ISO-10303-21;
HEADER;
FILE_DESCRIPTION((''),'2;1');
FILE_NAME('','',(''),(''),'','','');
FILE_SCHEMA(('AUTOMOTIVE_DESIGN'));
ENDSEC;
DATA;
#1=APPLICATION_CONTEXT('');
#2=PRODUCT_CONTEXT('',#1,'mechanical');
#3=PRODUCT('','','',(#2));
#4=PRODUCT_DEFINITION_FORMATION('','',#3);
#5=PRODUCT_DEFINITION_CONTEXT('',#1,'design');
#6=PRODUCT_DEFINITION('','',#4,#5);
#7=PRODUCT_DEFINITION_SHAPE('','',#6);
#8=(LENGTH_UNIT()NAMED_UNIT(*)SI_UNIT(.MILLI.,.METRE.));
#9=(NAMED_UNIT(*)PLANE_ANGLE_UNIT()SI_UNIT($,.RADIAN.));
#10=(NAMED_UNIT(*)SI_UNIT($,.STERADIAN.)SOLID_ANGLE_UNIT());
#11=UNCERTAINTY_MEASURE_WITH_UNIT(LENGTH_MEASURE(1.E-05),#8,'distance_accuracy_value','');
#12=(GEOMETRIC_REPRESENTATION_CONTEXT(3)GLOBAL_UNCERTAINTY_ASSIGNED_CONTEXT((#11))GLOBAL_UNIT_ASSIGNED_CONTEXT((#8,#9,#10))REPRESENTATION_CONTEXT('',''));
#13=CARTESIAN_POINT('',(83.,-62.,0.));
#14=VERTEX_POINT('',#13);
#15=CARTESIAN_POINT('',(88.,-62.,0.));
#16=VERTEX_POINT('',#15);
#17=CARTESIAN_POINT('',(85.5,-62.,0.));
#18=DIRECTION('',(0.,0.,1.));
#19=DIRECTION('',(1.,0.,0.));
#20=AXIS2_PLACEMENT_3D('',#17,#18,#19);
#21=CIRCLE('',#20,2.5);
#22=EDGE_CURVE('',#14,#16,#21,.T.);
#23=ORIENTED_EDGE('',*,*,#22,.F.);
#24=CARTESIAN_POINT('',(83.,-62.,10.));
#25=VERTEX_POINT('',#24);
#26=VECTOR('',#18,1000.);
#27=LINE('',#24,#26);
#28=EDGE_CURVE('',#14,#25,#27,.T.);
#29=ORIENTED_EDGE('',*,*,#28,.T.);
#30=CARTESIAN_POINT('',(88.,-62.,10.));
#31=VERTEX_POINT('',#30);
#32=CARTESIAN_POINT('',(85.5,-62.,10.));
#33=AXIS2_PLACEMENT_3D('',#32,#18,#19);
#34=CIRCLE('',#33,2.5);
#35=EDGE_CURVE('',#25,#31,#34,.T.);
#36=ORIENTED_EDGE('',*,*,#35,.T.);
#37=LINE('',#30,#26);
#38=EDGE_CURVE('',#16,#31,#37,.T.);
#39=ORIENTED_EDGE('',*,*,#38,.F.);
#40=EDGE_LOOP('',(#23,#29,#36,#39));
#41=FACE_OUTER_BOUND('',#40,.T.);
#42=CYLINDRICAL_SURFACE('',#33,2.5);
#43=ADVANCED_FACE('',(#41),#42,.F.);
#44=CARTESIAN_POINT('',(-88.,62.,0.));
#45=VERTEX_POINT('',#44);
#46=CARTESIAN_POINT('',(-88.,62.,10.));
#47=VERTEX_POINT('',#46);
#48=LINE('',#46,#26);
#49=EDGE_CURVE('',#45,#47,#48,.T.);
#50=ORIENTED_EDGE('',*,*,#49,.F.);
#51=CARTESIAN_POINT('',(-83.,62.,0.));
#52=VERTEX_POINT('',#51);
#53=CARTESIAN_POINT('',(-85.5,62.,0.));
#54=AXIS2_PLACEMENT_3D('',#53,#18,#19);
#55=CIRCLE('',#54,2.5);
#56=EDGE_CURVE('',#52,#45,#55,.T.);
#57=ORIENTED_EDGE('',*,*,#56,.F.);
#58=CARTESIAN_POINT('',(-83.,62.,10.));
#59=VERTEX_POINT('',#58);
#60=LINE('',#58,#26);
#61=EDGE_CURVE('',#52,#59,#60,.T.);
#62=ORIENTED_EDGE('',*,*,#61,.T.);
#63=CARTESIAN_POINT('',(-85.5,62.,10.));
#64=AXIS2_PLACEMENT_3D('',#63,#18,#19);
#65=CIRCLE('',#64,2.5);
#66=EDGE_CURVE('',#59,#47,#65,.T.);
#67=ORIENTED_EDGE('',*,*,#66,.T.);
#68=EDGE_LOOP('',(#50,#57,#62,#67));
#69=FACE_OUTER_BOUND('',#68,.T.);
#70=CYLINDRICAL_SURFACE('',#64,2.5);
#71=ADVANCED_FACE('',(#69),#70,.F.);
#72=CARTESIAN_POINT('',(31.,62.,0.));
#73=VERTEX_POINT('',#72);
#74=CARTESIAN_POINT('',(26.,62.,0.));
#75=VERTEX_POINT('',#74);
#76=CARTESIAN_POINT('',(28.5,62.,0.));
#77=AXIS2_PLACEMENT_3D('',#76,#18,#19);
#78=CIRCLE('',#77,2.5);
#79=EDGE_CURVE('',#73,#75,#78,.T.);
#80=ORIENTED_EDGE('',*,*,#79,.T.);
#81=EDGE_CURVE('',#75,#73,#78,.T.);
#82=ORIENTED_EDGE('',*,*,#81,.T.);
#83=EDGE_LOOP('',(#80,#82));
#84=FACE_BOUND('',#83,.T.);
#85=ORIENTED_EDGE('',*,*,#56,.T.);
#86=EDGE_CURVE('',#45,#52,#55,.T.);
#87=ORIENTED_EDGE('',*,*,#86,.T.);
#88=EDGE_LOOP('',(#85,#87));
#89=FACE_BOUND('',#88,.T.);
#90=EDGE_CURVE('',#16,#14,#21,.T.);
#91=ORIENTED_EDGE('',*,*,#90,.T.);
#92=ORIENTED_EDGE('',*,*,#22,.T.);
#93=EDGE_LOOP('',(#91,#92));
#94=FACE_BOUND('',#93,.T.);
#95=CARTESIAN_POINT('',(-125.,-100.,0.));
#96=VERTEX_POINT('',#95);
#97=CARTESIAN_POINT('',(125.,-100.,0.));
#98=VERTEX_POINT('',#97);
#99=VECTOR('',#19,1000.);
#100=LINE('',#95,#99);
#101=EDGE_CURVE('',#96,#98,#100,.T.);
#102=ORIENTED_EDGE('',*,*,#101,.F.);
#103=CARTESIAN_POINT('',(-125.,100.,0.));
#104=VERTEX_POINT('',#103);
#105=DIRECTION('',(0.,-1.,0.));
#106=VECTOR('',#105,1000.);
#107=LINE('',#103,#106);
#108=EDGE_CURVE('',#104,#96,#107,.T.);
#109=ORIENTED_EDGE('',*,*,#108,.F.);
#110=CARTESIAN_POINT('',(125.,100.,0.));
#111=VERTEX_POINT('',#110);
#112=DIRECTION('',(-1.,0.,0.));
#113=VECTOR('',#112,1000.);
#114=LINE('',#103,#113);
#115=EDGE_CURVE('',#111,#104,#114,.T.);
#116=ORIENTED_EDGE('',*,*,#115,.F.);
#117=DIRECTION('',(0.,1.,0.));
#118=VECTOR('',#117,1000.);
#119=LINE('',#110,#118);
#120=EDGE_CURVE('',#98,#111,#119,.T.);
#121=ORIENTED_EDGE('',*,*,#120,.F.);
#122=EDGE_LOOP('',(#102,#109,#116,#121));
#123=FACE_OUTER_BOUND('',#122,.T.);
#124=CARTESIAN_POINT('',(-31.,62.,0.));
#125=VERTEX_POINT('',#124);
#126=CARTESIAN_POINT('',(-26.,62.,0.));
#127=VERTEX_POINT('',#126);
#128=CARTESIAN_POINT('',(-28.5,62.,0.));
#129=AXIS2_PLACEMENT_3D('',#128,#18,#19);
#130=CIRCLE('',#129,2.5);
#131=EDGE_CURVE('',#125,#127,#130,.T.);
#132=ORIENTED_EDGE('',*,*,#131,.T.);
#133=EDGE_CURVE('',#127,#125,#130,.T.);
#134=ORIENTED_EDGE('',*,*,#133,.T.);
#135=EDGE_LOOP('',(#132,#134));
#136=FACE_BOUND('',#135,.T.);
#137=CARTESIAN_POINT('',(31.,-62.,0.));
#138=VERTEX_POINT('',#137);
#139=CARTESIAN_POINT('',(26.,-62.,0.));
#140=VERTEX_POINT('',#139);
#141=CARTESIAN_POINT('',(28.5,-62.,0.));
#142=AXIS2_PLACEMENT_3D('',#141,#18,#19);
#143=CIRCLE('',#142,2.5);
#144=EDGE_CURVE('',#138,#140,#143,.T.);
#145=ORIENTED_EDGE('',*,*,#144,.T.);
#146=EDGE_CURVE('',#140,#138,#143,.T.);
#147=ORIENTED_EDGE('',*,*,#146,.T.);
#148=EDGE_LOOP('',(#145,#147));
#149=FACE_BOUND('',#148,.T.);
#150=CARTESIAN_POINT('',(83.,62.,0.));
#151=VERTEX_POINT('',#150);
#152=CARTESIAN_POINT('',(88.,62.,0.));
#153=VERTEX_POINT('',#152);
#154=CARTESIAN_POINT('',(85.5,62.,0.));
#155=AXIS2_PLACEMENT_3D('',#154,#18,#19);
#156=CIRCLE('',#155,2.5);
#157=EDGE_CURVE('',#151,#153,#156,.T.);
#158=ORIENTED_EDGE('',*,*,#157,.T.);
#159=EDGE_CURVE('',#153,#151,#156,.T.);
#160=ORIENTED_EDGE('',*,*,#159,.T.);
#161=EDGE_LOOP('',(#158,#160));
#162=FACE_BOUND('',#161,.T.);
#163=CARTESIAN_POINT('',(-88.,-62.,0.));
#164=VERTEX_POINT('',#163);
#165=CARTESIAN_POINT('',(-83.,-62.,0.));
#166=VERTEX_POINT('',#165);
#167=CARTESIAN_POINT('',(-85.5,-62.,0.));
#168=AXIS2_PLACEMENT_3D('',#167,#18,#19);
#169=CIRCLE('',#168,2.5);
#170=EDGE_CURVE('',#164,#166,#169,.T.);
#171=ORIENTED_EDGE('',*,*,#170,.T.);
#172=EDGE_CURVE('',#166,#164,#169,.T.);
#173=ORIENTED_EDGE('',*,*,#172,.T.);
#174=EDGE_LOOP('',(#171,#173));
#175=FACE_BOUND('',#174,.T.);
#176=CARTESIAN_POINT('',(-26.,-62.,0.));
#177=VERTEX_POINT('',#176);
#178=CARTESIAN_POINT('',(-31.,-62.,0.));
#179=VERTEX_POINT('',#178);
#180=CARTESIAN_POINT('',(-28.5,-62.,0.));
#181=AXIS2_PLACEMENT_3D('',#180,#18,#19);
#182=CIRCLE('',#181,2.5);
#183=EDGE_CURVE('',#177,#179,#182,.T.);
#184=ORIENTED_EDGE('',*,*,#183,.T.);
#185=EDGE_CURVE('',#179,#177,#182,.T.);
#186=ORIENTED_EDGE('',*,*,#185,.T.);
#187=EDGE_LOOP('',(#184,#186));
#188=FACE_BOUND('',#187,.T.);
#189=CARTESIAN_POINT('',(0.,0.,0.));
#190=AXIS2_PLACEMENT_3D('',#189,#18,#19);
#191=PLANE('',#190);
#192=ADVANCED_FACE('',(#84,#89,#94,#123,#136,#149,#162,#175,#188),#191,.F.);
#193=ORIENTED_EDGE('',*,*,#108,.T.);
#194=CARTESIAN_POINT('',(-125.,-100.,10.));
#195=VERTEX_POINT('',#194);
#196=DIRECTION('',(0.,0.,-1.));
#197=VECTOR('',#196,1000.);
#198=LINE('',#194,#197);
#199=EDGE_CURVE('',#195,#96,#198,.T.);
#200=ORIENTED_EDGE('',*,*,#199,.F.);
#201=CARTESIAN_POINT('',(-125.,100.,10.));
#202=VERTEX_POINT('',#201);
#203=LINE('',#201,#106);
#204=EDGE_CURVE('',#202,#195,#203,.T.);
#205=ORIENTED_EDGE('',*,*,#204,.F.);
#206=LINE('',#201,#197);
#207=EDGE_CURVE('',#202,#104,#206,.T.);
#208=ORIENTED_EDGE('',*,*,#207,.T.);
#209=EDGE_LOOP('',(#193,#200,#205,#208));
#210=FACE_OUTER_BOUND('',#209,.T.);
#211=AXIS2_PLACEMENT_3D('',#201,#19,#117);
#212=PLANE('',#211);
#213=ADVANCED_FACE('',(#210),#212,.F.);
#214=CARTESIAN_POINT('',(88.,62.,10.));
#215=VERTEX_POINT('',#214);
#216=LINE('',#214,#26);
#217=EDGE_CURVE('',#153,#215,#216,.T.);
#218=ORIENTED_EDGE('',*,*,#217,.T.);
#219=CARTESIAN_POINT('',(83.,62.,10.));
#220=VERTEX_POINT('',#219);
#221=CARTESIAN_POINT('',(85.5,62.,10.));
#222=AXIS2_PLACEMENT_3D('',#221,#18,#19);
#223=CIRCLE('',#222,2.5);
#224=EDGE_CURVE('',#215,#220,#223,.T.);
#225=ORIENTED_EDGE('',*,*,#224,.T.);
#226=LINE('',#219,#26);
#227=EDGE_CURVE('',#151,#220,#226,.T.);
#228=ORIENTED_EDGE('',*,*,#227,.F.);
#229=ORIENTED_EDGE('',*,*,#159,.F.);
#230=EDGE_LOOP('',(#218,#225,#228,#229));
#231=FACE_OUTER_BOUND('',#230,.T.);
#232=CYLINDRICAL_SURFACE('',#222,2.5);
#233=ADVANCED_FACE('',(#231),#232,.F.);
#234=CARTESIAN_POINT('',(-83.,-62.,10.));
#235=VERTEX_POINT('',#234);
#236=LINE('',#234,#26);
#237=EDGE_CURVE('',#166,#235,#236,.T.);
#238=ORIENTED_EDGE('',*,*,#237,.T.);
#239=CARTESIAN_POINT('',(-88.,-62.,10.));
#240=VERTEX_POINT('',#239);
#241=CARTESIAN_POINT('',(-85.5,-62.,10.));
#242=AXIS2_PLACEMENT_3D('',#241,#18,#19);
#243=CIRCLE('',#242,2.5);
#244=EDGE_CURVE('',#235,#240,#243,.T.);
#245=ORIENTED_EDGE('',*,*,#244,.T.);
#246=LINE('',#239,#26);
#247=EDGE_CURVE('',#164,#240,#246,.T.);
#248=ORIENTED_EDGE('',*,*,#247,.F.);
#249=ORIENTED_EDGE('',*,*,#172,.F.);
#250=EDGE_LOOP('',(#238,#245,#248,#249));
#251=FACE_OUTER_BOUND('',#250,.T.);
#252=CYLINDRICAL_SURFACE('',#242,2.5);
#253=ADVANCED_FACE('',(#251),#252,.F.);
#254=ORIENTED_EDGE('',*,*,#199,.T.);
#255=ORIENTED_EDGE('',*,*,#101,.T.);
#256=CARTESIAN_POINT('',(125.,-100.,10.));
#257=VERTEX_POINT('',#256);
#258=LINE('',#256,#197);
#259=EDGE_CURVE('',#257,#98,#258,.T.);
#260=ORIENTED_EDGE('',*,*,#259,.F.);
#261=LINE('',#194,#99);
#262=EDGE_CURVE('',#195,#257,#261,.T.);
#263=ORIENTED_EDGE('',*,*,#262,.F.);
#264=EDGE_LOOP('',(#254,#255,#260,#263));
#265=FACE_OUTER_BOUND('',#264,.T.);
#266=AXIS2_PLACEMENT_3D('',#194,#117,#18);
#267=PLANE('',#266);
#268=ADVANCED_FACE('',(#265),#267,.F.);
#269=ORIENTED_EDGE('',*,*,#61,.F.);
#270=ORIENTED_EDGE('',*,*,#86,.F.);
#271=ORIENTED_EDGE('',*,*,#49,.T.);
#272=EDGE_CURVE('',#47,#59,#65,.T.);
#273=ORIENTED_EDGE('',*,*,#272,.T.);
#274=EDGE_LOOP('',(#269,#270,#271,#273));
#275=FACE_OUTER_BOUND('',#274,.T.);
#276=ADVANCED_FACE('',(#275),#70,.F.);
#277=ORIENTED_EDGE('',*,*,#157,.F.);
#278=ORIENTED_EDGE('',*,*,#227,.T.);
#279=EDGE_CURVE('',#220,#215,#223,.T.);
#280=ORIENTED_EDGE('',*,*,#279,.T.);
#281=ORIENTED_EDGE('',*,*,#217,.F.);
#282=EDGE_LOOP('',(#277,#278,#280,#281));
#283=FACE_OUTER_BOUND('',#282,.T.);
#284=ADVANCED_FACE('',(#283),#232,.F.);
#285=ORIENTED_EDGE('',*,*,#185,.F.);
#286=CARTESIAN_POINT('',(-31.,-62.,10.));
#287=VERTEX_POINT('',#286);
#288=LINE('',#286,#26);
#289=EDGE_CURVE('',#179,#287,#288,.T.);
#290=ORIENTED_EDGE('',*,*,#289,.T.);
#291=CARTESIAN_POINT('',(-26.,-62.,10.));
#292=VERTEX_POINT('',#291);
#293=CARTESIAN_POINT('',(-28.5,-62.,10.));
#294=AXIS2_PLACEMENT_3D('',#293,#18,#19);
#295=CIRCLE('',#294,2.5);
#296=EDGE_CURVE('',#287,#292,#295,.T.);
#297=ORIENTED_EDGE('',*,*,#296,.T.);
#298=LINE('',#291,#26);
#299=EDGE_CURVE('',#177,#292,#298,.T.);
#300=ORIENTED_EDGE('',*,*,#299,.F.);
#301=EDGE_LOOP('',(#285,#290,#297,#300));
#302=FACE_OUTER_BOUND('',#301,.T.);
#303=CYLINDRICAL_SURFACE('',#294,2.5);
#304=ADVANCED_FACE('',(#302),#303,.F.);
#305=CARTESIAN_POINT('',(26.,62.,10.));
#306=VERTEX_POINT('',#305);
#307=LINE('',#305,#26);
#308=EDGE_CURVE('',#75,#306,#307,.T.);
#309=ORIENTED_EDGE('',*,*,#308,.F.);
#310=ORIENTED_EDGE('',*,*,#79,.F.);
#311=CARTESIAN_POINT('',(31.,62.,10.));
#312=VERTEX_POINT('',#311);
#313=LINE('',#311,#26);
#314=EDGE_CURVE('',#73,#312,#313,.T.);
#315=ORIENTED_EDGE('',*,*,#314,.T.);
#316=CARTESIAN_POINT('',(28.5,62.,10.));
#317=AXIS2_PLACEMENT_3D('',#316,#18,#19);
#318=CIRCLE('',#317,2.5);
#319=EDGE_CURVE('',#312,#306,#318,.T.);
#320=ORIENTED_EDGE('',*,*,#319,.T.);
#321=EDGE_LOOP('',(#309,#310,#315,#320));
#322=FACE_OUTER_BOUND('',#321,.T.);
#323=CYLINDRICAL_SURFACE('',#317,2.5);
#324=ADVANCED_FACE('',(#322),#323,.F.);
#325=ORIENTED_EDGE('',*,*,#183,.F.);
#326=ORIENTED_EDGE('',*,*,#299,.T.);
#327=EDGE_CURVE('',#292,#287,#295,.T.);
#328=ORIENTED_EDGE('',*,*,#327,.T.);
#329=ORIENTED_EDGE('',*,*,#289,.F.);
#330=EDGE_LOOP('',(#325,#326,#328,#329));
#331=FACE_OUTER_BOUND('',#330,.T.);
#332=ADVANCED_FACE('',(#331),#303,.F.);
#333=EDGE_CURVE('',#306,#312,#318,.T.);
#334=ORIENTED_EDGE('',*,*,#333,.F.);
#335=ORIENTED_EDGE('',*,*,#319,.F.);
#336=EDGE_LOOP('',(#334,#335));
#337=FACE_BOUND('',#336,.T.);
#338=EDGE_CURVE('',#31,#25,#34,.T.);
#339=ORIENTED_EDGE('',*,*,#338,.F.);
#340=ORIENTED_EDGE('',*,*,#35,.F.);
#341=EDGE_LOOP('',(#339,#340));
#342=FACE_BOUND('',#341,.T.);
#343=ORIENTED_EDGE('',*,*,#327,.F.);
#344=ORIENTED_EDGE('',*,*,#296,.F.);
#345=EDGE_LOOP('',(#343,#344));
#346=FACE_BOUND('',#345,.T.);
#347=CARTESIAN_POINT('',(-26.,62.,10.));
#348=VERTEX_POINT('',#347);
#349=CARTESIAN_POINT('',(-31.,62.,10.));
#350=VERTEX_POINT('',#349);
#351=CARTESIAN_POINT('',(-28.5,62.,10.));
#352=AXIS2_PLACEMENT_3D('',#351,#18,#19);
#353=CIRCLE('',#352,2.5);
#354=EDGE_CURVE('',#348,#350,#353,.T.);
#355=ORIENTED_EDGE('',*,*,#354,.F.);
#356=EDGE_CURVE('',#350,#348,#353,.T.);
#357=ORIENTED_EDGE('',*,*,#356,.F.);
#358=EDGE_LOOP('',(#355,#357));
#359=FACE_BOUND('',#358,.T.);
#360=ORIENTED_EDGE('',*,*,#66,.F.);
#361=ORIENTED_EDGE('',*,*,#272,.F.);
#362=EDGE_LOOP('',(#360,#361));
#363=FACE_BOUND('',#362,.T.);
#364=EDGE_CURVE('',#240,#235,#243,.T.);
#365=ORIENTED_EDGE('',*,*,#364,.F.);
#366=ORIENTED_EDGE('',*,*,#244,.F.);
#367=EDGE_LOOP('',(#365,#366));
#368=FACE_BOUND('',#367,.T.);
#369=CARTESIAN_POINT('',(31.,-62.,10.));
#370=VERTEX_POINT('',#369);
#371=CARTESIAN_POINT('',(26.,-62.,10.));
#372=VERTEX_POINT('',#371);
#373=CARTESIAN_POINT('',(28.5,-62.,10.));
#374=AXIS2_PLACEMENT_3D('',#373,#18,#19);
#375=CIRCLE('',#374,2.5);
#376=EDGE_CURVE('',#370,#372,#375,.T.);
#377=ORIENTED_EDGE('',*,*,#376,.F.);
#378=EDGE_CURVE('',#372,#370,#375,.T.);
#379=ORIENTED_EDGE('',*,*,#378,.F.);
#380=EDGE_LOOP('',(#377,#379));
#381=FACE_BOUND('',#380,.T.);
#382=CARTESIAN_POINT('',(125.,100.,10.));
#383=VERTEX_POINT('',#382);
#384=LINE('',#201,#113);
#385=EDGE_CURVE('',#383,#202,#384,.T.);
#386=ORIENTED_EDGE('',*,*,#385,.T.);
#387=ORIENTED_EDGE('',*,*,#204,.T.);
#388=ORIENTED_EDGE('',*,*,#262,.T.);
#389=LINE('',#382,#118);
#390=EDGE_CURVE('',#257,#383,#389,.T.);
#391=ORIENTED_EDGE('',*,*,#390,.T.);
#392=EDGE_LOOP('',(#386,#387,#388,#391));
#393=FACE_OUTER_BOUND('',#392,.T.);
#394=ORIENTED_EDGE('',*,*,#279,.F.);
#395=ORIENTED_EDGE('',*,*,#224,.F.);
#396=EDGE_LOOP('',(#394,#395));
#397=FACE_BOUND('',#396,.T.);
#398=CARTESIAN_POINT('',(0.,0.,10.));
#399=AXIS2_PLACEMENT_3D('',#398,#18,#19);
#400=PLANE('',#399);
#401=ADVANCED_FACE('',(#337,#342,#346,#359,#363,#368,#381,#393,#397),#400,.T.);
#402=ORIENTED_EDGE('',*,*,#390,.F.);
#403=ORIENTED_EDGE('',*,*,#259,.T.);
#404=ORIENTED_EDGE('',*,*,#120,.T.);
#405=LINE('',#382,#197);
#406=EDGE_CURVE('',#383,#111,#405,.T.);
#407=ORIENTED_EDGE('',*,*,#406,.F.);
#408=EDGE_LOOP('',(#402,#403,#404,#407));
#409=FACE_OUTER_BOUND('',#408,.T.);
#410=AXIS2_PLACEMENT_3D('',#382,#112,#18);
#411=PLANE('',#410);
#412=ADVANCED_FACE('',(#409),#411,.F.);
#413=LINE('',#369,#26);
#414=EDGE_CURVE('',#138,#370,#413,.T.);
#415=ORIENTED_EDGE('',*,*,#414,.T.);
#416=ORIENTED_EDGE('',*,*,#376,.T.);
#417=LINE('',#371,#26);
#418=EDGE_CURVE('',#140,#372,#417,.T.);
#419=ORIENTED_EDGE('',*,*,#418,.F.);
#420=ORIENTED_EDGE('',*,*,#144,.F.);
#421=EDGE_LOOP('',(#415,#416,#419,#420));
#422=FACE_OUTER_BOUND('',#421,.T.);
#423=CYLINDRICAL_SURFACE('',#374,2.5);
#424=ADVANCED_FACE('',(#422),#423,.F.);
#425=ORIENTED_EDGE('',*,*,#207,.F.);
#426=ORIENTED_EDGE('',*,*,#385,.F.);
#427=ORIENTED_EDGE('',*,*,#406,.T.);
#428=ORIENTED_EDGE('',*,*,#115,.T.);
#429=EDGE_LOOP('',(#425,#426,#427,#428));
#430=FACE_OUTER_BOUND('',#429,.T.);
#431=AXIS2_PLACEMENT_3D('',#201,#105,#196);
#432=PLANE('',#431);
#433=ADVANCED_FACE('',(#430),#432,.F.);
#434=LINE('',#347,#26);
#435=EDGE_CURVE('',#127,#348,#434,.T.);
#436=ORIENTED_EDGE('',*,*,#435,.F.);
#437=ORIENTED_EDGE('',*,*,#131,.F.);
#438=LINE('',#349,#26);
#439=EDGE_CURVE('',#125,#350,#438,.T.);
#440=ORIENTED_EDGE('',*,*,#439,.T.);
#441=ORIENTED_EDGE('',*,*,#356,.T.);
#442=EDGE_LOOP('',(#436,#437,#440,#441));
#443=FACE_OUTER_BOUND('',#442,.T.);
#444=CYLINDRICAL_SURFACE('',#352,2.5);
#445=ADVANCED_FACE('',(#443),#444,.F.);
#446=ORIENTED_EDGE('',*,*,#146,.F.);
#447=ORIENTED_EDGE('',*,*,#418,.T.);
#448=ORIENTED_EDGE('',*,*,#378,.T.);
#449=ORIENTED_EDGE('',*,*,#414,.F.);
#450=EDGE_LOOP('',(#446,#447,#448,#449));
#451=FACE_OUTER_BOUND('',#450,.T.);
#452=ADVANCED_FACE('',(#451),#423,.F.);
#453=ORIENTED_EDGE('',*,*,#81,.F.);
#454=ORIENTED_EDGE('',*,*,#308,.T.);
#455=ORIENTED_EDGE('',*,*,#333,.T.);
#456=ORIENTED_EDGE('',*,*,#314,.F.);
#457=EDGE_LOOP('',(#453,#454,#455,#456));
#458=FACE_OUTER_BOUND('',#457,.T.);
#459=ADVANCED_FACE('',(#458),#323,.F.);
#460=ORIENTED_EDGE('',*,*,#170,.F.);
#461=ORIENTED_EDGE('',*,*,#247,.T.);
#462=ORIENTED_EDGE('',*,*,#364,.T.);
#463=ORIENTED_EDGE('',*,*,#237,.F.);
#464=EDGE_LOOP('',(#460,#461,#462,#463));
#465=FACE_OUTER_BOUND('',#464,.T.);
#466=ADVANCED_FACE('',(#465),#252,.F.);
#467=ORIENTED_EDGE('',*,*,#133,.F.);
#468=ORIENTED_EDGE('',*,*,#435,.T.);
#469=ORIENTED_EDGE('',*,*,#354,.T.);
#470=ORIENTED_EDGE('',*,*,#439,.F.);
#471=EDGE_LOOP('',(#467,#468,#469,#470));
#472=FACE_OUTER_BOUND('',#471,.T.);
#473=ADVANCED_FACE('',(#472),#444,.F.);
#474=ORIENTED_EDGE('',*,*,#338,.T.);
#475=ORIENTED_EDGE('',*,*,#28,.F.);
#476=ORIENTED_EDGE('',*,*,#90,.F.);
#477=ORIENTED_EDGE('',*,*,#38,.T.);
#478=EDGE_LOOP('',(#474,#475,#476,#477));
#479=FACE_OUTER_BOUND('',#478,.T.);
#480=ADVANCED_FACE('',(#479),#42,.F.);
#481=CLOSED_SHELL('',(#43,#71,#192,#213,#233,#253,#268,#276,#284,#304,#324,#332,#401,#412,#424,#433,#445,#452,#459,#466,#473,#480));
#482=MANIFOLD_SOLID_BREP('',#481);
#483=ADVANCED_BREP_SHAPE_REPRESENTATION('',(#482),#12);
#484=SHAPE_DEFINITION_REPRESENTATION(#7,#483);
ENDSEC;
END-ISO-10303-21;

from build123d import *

# Parameters (mm, degrees)
SKETCH1_W           = 250
SKETCH1_H           = 200
BOSS_EXTRUDE1_DEPTH = 10
M6_TAPPED_HOLE1_D   = 5


with BuildPart() as part:
    # Sketch1 → Boss-Extrude1 (new body)
    with BuildSketch(Plane.XY):
        Rectangle(SKETCH1_W, SKETCH1_H)
    extrude(amount=BOSS_EXTRUDE1_DEPTH)

    # M6 Tapped Hole1 (through all)
    with Locations(Plane.XY.offset(10)):
        with Locations((-85.5, 62), (-28.5, 62), (85.5, 62), (28.5, 62), (28.5, -62), (85.5, -62), (-28.5, -62), (-85.5, -62)):
            Hole(M6_TAPPED_HOLE1_D / 2)


solid = part.part
